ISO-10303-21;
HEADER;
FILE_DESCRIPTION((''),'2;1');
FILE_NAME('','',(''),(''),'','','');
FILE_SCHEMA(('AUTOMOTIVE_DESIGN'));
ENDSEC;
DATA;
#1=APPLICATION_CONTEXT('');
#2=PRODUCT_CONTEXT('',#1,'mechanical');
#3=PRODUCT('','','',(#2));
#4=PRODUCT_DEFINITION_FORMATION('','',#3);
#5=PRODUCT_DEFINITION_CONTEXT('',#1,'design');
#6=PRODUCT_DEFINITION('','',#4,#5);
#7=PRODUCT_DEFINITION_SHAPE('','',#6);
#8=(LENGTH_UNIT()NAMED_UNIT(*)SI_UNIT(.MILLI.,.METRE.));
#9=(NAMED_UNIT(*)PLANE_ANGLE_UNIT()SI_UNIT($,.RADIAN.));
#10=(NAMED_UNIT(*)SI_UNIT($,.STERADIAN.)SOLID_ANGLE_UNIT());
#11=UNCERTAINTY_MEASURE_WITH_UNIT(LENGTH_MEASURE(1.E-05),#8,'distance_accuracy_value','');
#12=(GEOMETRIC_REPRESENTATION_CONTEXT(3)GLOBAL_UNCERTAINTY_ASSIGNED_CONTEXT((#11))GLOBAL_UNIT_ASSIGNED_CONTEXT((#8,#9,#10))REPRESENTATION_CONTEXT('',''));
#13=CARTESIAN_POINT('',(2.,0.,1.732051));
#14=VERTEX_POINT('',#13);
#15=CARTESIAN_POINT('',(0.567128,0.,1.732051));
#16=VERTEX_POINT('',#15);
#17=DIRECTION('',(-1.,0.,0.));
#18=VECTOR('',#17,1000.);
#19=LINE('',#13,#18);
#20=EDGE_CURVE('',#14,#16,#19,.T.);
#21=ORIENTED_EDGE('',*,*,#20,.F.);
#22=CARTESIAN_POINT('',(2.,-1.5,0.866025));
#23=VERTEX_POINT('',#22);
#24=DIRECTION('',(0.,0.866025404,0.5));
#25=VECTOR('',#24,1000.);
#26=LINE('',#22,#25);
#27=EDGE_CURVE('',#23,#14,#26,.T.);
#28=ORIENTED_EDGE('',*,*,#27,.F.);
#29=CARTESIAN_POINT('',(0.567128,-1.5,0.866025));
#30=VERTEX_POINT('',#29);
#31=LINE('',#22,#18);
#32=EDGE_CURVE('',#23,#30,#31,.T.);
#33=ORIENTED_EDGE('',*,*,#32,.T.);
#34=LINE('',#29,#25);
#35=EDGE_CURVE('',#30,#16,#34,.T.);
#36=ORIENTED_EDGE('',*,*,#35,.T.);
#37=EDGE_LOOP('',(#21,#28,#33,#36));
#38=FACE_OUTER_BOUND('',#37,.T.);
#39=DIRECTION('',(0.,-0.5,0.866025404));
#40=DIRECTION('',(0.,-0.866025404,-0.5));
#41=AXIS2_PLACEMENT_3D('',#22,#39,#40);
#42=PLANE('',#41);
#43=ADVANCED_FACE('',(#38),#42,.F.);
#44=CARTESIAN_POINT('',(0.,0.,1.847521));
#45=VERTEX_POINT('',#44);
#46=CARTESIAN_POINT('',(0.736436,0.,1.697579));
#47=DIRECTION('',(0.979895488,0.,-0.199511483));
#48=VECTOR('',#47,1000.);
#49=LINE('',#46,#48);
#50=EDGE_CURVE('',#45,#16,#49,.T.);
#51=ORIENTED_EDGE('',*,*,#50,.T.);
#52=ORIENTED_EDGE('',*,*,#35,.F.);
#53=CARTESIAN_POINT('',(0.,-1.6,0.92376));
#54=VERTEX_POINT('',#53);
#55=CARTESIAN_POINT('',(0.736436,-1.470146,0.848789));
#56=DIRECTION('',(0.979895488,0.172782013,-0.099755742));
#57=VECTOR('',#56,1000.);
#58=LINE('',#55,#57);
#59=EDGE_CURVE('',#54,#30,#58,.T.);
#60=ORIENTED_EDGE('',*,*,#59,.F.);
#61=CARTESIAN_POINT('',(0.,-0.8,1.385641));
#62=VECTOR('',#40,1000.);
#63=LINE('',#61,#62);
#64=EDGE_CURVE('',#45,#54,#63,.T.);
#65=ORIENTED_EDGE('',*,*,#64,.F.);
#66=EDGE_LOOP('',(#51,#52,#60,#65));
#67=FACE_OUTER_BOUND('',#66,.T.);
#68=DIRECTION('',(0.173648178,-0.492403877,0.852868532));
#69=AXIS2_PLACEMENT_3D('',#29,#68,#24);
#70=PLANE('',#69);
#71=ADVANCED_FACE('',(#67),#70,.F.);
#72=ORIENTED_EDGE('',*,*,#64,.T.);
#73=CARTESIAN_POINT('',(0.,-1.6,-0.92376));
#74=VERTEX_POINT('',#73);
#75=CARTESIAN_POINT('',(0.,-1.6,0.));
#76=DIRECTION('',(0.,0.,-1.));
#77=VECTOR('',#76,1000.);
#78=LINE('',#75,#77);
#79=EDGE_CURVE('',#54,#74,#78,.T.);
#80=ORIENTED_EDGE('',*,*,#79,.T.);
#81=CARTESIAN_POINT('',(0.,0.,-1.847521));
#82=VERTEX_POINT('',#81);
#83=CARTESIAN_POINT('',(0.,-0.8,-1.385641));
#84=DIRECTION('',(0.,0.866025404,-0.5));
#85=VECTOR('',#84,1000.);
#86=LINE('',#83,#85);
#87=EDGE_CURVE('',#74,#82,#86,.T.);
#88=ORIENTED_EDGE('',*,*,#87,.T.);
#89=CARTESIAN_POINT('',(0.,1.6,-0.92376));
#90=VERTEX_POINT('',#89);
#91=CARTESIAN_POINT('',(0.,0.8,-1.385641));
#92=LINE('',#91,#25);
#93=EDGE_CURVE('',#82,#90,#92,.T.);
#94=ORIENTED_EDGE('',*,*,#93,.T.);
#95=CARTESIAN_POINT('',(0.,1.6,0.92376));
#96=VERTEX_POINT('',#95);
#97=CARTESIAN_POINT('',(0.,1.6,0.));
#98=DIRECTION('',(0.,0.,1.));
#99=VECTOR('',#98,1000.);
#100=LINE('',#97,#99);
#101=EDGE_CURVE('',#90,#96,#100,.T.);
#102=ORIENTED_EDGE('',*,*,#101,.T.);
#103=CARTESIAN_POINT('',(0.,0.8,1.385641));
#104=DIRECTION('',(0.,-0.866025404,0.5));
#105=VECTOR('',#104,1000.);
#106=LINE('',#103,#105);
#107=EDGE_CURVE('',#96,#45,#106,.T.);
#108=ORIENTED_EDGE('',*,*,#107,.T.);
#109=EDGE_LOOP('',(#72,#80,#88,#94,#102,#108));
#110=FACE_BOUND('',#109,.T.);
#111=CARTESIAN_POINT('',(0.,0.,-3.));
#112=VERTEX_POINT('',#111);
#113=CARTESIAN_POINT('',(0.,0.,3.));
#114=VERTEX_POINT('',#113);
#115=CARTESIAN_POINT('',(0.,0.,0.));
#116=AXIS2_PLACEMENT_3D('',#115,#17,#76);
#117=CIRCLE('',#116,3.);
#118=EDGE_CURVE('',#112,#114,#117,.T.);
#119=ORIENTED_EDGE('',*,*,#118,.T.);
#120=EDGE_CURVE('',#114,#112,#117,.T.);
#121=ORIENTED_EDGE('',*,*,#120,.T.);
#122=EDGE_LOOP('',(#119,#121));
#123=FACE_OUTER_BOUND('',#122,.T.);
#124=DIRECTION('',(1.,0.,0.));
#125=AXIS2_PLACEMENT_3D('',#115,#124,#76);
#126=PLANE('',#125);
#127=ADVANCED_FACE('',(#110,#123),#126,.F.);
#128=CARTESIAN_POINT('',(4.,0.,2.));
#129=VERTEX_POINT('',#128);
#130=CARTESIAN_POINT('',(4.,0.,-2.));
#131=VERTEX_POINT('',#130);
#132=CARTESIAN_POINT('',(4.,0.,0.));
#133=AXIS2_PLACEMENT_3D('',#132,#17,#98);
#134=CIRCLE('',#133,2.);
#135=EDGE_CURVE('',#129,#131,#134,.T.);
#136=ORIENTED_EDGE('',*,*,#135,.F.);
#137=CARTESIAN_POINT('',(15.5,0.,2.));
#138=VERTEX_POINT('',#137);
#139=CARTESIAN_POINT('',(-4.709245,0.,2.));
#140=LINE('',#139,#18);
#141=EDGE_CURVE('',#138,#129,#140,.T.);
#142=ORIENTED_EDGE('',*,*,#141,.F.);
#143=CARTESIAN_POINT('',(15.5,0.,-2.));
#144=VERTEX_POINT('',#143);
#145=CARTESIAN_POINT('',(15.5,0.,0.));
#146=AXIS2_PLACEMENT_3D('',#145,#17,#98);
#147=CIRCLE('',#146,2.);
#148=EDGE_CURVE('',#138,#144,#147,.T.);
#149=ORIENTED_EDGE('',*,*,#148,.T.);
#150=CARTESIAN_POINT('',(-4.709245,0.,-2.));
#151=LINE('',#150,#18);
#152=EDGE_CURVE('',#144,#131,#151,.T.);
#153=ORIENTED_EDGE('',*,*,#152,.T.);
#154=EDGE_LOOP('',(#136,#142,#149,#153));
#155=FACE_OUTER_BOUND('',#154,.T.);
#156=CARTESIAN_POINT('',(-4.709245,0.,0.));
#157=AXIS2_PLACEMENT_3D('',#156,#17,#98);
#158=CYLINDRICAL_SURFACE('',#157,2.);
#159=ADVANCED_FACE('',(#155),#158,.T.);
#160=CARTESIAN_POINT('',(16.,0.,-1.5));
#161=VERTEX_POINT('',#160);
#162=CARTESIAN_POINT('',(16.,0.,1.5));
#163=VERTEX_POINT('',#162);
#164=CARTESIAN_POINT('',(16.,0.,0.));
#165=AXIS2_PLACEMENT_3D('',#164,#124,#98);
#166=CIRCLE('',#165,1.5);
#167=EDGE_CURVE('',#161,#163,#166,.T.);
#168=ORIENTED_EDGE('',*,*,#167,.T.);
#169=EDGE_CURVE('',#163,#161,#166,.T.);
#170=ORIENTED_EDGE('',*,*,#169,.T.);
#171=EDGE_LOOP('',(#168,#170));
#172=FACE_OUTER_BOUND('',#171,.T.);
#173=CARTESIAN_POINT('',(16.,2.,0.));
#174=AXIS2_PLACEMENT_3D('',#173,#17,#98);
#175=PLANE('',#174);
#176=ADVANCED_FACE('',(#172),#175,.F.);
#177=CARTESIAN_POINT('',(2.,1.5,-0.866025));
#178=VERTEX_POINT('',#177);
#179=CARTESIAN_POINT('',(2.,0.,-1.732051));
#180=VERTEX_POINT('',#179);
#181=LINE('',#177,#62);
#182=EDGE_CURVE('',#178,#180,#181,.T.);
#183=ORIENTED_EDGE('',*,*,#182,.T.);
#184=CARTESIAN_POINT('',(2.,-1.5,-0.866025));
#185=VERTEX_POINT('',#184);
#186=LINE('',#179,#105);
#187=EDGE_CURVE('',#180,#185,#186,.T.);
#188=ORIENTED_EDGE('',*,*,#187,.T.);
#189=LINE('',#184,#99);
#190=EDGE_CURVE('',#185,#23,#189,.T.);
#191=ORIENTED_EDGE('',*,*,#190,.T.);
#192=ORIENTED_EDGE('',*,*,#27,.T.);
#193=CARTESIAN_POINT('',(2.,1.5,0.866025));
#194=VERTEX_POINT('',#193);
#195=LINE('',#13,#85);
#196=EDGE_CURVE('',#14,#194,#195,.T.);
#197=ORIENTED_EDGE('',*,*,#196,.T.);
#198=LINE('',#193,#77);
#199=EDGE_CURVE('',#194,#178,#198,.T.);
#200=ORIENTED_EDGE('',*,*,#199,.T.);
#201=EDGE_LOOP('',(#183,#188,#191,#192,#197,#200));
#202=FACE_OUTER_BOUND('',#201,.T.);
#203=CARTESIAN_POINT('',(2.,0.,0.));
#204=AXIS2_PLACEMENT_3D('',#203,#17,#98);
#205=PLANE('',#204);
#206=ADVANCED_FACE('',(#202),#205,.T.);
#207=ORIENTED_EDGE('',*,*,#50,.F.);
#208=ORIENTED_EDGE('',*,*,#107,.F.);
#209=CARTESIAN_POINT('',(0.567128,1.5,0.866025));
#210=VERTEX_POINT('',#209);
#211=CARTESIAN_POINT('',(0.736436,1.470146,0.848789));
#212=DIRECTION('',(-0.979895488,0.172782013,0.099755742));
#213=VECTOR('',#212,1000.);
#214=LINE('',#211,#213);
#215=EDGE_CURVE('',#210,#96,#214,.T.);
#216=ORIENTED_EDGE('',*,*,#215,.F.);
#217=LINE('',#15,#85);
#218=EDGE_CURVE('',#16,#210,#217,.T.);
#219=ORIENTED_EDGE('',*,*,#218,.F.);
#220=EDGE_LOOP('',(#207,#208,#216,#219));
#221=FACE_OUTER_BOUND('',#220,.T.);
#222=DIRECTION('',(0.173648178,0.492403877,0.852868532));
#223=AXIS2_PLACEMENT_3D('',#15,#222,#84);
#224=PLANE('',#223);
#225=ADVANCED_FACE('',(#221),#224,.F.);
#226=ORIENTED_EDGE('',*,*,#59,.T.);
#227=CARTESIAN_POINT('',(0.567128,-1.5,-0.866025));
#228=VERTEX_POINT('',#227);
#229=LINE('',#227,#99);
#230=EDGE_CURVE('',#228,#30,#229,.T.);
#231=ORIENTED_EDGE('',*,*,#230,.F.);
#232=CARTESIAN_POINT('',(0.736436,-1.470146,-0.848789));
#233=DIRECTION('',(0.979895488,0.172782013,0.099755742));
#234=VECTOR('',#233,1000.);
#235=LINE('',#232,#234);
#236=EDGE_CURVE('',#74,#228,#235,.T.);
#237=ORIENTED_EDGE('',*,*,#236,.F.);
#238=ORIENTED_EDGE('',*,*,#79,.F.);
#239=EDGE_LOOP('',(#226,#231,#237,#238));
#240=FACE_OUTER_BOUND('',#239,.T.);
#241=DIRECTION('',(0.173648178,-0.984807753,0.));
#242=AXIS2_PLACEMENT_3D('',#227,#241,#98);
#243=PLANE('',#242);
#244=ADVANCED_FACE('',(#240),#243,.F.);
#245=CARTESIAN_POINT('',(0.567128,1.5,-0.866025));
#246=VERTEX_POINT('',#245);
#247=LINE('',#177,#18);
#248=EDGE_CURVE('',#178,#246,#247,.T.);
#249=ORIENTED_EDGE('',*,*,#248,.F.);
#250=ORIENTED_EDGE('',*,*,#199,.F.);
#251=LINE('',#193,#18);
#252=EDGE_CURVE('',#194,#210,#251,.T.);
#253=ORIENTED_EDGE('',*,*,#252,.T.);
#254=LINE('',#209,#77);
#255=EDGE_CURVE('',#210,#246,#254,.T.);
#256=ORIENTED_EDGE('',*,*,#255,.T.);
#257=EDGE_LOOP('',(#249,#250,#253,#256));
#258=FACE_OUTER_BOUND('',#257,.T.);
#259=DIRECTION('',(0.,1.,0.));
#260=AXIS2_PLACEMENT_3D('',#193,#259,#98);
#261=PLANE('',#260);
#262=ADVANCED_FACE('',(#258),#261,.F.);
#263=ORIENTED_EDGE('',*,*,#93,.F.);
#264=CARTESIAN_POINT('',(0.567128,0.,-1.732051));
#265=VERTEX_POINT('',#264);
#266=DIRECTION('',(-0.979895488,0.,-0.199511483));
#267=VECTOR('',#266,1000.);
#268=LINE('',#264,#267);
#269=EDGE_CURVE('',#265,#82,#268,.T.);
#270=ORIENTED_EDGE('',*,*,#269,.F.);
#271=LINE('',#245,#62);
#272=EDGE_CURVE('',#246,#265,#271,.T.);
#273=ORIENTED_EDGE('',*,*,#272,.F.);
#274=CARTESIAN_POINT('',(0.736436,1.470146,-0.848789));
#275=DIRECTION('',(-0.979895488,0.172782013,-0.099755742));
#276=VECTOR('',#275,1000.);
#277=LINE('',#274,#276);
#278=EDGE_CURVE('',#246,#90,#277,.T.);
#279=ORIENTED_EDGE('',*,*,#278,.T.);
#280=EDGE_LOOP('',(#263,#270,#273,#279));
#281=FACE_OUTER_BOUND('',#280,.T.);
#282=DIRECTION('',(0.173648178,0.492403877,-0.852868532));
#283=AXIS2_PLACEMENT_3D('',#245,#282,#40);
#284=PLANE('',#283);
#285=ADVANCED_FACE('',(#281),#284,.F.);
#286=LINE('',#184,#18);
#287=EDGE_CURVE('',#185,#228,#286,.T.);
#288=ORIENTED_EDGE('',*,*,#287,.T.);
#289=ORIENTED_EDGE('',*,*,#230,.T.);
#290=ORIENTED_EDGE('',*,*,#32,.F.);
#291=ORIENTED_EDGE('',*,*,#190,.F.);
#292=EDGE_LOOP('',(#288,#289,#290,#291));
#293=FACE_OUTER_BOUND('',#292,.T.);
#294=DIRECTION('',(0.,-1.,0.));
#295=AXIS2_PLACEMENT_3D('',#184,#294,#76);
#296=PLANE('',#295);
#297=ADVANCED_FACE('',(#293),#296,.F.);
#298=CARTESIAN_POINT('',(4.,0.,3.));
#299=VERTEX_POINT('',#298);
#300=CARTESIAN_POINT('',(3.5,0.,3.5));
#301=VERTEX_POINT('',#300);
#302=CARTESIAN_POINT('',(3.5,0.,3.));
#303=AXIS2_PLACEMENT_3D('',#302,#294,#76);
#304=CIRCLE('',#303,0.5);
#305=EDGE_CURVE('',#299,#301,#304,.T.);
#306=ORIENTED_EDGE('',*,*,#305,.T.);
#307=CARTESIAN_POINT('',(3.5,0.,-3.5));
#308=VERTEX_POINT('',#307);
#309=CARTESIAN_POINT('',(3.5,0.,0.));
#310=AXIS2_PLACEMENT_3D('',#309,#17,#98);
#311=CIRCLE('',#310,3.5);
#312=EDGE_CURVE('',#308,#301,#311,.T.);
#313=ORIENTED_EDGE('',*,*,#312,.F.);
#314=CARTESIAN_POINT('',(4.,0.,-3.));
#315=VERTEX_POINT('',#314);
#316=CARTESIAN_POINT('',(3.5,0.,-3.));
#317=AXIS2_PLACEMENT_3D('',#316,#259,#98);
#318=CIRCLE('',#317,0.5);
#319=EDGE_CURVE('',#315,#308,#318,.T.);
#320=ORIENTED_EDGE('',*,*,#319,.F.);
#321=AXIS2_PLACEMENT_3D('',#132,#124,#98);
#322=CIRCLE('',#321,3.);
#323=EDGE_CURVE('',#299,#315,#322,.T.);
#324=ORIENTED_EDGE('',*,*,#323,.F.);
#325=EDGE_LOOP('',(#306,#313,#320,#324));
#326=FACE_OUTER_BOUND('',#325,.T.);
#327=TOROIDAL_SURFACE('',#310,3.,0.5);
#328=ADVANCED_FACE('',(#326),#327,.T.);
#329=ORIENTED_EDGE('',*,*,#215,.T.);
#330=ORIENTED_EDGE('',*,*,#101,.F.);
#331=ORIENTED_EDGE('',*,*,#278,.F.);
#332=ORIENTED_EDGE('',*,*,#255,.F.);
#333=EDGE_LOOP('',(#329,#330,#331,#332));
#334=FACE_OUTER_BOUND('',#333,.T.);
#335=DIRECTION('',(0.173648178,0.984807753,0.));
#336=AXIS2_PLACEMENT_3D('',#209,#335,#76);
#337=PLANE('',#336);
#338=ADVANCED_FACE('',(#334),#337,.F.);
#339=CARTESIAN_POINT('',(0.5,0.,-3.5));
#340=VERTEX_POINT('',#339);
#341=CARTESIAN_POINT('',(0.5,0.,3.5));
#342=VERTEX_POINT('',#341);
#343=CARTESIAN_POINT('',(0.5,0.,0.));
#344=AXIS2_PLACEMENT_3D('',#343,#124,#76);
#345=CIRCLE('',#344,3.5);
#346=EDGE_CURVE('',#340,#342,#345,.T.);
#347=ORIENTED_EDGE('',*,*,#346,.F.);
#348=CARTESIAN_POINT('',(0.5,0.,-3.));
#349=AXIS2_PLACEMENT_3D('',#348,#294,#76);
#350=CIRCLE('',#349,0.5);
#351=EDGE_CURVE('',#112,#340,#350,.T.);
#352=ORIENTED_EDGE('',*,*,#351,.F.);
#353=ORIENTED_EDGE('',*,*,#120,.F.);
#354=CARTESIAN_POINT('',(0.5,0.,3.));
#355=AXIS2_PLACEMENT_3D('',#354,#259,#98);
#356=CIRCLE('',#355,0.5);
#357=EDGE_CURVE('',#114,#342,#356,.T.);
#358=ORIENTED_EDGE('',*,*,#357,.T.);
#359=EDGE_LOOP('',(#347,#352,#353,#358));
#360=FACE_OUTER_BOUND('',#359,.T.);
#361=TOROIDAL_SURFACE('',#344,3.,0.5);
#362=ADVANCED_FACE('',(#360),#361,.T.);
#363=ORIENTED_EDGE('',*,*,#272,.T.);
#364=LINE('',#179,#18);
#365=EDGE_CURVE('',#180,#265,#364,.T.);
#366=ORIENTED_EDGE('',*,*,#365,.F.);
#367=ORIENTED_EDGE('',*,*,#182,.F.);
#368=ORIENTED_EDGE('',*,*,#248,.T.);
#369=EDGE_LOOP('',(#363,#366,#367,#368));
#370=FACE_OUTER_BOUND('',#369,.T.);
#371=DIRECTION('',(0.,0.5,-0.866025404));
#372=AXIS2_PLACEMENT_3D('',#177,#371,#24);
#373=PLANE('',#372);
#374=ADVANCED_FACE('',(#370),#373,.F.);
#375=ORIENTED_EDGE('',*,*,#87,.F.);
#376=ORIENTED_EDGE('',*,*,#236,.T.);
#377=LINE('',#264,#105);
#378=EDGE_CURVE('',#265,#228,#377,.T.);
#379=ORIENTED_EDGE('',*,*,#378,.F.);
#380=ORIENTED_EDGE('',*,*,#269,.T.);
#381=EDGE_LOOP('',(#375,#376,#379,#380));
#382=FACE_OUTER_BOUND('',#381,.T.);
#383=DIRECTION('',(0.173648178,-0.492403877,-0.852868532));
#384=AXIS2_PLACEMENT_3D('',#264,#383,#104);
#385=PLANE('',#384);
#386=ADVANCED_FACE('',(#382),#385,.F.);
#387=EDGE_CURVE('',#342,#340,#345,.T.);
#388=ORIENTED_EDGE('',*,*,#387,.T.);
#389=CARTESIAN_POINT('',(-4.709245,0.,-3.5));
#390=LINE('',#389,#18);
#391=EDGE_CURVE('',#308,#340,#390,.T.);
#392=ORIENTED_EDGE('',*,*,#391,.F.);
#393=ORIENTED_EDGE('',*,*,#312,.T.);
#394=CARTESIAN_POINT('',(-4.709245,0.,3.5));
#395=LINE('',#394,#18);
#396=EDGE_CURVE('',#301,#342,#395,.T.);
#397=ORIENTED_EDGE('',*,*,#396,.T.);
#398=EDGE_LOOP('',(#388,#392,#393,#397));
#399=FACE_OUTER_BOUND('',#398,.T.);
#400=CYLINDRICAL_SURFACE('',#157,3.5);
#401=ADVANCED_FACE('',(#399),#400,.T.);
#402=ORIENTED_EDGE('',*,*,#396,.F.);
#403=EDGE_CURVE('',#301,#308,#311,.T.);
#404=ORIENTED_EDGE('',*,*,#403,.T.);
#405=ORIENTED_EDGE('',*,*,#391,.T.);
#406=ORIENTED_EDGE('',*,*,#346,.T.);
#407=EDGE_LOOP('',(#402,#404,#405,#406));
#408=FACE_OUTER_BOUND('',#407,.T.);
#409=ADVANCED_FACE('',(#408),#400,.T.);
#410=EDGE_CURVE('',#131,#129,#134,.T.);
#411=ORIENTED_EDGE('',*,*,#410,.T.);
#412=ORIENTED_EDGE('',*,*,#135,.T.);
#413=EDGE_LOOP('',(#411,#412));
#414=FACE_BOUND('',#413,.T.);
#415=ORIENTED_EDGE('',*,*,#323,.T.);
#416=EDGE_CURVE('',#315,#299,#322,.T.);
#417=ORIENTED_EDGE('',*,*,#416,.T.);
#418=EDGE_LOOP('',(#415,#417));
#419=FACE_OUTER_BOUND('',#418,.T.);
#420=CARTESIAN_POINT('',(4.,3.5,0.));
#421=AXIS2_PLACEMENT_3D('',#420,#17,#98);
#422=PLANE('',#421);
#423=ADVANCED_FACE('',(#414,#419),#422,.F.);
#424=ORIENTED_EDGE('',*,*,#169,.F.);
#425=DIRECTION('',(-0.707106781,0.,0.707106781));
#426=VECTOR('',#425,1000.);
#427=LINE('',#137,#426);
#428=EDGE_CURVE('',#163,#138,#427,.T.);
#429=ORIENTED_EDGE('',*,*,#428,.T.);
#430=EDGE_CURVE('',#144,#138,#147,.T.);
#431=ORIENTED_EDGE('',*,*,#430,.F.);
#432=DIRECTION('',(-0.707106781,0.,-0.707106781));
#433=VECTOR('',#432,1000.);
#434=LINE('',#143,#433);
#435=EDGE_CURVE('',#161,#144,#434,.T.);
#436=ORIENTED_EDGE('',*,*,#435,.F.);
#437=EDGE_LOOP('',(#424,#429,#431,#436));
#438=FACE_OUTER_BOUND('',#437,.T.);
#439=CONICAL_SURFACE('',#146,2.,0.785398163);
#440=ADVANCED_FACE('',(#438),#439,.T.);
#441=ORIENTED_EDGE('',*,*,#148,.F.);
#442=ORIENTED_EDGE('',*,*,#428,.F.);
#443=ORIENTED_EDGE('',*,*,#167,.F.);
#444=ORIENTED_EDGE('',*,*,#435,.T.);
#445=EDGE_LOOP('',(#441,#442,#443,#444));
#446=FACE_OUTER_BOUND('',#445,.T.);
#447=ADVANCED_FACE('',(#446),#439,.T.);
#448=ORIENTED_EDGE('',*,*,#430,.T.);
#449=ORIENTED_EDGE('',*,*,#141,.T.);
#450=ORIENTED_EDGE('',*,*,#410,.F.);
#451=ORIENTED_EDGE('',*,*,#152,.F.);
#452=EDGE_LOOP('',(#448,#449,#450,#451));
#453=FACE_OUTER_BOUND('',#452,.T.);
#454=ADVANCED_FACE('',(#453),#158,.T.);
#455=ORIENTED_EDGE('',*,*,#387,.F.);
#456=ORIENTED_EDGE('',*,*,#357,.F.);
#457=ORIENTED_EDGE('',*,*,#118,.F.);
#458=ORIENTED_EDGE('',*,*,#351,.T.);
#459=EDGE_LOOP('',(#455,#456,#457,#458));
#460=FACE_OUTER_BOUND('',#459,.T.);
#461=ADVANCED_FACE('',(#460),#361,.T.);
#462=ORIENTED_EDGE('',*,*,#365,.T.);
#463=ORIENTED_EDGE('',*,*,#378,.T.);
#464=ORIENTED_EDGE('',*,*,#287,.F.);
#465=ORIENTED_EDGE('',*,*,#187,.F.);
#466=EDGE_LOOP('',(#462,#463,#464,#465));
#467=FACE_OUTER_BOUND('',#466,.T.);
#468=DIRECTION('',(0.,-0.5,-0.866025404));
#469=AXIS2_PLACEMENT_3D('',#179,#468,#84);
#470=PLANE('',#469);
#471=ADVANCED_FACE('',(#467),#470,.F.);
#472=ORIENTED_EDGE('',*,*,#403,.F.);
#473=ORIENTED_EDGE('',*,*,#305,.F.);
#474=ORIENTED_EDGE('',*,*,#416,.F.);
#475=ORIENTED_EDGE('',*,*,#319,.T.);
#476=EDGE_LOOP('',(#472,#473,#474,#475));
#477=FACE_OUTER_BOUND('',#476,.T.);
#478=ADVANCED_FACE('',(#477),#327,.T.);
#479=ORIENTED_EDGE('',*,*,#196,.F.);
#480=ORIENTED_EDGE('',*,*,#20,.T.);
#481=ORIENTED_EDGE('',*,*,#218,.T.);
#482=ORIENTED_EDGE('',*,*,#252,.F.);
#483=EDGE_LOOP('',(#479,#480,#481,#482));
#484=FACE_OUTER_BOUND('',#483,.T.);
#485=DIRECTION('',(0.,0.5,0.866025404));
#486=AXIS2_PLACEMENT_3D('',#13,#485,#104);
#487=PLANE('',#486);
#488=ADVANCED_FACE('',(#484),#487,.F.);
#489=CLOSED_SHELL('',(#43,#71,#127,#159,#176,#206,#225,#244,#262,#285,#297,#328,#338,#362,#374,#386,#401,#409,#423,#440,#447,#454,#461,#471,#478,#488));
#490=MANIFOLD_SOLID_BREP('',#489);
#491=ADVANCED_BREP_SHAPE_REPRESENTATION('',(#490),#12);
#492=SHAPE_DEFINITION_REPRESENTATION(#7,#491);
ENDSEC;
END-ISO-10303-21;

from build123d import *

# Parameters (mm, degrees)
CUT_EXTRUDE1_DEPTH = 2
FILLET1_R          = 0.5
CHAMFER1_SIZE      = 0.1
CHAMFER1_SIZE2     = 0.567128182
CHAMFER2_SIZE      = 0.5


with BuildPart() as part:
    # Sketch1 → Revolve1 (revolve)
    with BuildSketch(Plane.XY, mode=Mode.PRIVATE) as revolve1_sk:
        Polygon((0, 0), (0, 3.5), (4, 3.5), (4, 2), (16, 2), (16, 0), align=None)
    revolve(revolve1_sk.sketch.rotate(Axis((-4.709244637, 0, 0), (1, 0, 0)), 90), axis=Axis((-4.709244637, 0, 0), (1, 0, 0)))

    # Sketch4 → Cut-Extrude1 (cut)
    with BuildSketch(Plane.ZY):
        Polygon((-1.732050808, 0), (-0.866025404, -1.5), (0.866025404, -1.5), (1.732050808, 0), (0.866025404, 1.5), (-0.866025404, 1.5), align=None)
    extrude(amount=-CUT_EXTRUDE1_DEPTH, mode=Mode.SUBTRACT)

    # Fillet1
    fillet1_edges = [part.edges().sort_by_distance(p)[0] for p in [
        (4, 0, -3.5),
        (0, 0, -3.5),
    ]]
    fillet(fillet1_edges, radius=FILLET1_R)

    # Chamfer1
    chamfer1_edges = [part.edges().sort_by_distance(p)[0] for p in [
        (0, 0.75, -1.299038106),
        (0, -0.75, -1.299038106),
        (0, -1.5, 0),
        (0, -0.75, 1.299038106),
        (0, 0.75, 1.299038106),
        (0, 1.5, 0),
    ]]
    chamfer1_side = [part.faces().sort_by_distance(p)[0] for p in [
        (0, 0, -2.915147186),
    ]]
    chamfer(chamfer1_edges, length=CHAMFER1_SIZE, length2=CHAMFER1_SIZE2, reference=chamfer1_side[0])

    # Chamfer2
    chamfer2_edges = [part.edges().sort_by_distance(p)[0] for p in [
        (16, 0, -2),
    ]]
    chamfer(chamfer2_edges, length=CHAMFER2_SIZE)


solid = part.part
